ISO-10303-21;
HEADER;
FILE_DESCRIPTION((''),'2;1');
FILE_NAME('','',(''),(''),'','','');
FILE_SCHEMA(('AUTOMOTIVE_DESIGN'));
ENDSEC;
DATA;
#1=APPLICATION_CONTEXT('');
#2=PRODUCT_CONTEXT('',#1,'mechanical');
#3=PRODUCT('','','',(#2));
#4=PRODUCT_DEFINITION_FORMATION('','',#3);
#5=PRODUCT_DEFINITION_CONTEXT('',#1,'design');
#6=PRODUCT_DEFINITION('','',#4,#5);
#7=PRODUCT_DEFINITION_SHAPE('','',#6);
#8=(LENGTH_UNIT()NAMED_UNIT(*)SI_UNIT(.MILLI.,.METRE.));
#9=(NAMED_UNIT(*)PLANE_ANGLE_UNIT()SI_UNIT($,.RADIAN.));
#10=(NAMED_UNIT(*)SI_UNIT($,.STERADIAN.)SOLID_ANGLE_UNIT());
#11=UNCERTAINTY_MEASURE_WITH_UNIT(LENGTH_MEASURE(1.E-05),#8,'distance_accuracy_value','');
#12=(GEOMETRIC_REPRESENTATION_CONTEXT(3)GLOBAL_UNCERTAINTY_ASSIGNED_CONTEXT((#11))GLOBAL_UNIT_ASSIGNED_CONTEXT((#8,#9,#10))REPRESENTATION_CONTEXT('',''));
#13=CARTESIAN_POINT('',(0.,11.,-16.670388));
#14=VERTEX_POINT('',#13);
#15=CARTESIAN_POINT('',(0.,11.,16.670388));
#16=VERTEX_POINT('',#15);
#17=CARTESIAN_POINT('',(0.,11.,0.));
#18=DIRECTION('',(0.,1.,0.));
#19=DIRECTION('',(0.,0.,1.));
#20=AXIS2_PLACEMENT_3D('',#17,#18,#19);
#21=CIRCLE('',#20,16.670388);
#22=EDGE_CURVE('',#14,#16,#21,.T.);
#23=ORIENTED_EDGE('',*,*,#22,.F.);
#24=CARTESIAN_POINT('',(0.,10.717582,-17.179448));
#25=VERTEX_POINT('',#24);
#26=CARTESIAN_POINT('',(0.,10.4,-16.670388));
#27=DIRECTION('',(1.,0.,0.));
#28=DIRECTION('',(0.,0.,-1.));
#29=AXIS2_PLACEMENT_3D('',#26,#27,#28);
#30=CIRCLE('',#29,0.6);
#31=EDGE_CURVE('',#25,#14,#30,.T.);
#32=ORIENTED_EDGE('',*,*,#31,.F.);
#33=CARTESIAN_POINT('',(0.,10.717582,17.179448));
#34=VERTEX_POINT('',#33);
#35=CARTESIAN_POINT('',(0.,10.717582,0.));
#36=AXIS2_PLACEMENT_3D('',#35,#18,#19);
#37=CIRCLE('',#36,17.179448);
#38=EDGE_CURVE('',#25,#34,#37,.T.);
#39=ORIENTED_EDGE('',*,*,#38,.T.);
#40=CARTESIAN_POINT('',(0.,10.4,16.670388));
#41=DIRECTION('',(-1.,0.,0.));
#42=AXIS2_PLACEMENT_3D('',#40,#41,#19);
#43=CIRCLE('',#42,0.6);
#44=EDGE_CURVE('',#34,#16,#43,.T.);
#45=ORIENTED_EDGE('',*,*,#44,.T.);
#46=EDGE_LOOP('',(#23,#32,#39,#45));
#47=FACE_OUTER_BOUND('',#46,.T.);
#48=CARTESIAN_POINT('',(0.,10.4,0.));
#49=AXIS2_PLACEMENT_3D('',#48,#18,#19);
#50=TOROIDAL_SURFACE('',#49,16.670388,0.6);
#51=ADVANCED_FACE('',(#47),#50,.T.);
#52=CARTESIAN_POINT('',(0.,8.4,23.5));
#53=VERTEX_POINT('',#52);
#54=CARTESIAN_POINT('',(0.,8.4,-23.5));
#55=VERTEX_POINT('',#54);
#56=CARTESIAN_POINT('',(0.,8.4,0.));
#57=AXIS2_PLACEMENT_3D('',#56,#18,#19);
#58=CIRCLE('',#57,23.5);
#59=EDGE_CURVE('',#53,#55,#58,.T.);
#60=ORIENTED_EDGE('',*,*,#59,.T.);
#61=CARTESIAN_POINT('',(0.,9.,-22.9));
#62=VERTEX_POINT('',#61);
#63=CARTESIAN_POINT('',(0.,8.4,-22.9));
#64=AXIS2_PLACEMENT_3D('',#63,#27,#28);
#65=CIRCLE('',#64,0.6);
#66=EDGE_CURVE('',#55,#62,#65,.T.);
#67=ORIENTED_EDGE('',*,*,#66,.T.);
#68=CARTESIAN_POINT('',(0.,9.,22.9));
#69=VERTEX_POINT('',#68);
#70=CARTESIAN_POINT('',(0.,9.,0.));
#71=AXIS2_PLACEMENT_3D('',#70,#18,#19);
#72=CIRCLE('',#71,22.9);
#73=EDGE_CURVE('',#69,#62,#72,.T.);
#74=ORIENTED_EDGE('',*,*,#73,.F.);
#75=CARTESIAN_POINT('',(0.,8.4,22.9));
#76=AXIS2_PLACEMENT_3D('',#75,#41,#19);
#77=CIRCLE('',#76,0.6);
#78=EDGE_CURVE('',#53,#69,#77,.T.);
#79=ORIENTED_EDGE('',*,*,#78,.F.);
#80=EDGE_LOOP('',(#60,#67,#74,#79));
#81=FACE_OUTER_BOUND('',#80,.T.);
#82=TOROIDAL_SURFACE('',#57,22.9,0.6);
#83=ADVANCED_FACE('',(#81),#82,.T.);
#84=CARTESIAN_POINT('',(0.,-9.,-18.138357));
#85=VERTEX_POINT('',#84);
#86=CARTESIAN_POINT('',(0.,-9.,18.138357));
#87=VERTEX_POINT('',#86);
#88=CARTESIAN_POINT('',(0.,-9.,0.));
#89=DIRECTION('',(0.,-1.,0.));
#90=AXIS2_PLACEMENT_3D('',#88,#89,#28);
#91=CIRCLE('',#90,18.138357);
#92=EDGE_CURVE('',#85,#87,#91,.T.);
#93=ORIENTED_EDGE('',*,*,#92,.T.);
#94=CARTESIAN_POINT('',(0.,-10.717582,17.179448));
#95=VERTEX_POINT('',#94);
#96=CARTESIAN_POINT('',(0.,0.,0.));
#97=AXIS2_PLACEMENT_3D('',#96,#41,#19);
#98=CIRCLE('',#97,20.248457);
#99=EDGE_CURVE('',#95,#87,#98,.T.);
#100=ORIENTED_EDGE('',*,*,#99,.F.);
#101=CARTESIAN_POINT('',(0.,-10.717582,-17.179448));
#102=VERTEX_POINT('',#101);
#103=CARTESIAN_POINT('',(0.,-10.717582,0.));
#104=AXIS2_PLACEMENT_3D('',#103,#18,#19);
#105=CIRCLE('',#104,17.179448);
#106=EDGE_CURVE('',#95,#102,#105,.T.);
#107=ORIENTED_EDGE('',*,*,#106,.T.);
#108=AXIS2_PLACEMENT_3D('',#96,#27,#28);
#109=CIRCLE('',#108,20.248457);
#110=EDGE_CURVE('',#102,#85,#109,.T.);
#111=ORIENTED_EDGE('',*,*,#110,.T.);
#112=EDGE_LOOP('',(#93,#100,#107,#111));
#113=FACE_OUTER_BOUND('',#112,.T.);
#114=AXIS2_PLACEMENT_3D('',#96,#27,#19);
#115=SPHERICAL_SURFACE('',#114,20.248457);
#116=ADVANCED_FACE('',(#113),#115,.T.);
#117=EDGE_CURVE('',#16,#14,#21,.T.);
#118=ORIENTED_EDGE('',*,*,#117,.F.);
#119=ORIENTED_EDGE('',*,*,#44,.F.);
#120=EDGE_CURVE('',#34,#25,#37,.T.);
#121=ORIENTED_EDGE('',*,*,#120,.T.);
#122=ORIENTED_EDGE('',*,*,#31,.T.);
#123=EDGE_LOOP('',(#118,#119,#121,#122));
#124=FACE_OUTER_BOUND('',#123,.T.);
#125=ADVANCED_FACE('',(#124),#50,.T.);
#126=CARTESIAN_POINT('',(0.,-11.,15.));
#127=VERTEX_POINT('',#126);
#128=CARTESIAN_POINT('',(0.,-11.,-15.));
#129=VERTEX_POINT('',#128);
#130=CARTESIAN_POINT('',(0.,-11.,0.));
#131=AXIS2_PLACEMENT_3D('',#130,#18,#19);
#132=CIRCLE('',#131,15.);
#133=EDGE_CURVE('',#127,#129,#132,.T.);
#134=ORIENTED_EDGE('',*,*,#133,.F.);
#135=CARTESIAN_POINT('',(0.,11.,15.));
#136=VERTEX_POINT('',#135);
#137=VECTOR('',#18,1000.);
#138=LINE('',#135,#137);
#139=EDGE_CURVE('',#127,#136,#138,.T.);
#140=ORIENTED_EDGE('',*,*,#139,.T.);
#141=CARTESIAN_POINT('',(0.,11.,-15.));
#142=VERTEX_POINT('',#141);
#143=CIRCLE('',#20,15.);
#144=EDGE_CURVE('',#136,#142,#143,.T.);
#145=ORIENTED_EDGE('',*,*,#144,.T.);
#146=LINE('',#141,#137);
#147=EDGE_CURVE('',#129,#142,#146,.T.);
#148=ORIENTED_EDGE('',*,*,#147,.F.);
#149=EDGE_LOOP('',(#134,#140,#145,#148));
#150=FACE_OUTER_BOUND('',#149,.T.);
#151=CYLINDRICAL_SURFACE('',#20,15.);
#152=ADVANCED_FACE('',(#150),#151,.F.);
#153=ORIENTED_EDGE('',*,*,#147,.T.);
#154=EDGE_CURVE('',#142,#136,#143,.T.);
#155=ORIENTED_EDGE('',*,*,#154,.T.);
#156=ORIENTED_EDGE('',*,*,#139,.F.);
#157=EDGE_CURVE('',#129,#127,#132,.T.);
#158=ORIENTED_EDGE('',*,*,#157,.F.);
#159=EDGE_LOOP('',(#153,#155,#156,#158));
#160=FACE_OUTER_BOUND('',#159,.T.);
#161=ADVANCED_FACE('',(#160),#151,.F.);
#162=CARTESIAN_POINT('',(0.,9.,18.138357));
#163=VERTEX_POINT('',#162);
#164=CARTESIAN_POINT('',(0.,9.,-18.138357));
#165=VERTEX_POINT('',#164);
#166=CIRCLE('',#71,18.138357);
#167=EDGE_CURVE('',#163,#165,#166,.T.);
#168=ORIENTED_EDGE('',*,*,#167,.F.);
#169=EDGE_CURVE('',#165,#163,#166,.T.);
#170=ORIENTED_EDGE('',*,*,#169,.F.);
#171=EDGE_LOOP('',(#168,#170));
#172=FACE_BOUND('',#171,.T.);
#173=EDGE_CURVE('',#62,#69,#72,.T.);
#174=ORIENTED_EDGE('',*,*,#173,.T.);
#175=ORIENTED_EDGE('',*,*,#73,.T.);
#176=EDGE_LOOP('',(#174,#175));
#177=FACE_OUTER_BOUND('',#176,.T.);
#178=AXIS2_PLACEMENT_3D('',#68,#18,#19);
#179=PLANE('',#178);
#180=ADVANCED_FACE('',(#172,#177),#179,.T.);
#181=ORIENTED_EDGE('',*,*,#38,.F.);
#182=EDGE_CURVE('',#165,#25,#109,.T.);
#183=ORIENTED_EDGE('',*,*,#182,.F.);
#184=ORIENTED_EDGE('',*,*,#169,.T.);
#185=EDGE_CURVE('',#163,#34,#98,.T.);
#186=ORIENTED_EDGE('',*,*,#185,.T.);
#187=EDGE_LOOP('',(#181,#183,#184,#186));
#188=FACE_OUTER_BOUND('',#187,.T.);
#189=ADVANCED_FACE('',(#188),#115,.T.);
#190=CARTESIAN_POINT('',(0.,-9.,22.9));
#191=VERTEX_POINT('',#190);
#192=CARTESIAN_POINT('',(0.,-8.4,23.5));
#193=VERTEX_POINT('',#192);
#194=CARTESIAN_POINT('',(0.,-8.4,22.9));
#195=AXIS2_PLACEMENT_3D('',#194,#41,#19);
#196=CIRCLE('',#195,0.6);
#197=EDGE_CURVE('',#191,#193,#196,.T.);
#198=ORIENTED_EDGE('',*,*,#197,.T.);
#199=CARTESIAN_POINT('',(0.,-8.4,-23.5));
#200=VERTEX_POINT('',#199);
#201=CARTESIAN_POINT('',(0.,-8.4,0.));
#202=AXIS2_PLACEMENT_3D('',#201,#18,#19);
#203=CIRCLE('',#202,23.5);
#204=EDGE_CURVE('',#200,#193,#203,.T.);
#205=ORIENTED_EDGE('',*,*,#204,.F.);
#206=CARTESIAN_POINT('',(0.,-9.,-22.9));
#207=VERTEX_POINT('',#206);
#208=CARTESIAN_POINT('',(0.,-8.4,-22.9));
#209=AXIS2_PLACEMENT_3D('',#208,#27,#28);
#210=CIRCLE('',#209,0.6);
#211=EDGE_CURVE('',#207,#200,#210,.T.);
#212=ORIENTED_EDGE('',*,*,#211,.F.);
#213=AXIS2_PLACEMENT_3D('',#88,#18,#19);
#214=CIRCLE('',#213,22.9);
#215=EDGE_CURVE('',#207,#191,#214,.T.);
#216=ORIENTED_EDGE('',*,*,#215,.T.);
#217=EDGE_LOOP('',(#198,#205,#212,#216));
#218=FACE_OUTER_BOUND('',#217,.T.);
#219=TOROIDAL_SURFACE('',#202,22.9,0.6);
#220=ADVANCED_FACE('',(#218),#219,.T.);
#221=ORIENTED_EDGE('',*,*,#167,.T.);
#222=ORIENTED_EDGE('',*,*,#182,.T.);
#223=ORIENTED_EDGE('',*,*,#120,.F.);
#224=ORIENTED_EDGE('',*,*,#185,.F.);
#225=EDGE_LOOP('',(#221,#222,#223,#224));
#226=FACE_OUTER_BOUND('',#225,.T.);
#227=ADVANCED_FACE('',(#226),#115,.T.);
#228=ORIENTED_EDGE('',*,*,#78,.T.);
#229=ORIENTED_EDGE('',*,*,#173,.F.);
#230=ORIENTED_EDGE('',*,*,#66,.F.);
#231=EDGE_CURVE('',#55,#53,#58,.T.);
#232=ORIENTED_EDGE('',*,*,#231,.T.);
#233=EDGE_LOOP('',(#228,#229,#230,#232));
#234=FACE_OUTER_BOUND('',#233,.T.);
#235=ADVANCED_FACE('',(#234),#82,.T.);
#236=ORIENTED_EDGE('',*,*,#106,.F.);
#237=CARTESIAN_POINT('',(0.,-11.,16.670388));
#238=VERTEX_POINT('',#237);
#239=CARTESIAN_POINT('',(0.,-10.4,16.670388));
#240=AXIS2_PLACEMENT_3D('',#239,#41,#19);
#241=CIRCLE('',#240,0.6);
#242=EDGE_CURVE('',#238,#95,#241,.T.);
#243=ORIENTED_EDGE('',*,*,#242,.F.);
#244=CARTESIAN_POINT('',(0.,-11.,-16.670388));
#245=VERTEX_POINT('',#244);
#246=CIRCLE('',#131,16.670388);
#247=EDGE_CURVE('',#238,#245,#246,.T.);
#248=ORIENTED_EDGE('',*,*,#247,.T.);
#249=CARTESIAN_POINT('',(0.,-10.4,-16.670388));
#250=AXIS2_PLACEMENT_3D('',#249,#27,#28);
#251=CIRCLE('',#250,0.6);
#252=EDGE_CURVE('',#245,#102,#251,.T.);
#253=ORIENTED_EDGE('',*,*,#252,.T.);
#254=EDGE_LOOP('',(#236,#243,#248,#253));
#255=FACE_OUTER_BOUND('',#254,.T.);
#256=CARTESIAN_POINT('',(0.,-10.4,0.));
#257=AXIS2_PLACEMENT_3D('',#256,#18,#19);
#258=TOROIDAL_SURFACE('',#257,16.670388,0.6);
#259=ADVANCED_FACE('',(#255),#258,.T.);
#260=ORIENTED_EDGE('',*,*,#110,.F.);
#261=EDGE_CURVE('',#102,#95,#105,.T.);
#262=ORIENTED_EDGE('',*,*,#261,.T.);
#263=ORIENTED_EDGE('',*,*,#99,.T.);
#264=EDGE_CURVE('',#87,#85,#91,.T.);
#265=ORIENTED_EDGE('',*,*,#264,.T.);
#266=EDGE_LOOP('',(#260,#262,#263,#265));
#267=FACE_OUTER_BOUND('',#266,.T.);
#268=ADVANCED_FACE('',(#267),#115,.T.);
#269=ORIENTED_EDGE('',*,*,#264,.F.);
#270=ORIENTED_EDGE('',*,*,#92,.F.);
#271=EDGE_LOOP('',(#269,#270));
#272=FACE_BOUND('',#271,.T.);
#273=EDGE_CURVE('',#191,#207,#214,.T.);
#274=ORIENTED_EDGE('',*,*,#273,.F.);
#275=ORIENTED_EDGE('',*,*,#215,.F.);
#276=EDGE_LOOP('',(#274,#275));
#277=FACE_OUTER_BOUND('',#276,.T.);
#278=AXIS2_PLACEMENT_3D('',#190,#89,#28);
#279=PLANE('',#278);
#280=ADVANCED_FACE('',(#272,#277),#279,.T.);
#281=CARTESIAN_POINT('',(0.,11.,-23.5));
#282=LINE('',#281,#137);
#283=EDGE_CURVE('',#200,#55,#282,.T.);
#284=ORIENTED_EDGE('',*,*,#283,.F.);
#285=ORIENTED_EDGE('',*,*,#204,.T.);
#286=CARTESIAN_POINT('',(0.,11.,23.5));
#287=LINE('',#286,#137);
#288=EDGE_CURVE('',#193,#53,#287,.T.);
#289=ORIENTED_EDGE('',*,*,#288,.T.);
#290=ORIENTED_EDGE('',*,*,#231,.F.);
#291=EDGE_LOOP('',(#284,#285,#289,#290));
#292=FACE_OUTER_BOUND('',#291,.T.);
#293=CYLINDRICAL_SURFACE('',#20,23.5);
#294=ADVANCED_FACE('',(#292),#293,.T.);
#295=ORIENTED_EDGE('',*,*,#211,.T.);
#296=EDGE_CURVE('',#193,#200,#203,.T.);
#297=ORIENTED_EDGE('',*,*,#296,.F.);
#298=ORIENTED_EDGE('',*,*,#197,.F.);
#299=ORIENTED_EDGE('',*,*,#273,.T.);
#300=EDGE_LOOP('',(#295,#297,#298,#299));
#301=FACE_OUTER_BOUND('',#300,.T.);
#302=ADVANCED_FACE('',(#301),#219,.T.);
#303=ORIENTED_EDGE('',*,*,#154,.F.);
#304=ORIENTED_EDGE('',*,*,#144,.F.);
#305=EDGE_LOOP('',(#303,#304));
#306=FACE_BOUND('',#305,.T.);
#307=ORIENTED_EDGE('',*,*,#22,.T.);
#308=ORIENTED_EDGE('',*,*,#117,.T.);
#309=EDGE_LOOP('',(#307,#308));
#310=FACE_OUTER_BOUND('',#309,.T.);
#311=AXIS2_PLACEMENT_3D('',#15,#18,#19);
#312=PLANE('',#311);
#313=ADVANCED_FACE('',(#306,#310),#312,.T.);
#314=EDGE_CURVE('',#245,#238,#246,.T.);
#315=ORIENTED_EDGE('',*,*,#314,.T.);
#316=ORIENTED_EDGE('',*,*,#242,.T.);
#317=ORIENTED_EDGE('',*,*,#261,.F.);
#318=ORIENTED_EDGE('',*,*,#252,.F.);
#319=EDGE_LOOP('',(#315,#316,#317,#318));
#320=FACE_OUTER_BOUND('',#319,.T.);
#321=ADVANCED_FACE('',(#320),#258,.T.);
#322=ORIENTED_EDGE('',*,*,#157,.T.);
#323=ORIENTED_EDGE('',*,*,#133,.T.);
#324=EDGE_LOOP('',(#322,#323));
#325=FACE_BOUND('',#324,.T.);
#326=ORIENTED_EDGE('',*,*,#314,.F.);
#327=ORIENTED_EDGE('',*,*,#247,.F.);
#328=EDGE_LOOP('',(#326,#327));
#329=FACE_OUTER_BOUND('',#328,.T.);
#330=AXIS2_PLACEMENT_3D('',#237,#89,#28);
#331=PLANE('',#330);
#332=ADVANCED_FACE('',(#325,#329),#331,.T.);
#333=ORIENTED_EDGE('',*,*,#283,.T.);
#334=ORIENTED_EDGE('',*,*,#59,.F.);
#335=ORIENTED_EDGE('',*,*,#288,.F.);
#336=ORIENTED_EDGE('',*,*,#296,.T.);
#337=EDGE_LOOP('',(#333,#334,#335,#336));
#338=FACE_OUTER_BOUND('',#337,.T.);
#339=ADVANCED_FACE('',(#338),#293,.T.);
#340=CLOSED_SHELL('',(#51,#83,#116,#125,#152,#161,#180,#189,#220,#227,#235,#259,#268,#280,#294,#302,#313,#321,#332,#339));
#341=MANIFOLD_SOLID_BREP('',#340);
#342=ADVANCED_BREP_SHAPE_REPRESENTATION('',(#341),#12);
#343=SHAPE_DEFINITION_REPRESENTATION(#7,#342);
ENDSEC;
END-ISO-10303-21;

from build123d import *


with BuildPart() as part:
    # 草图2 → 旋转1 (revolve)
    with BuildSketch(Plane(origin=(0, 0, 0), x_dir=(0, 0, -1), z_dir=(1, 0, 0))):
        with BuildLine():
            Line((-22.9, 9), (-18.138357147, 9))
            ThreePointArc((-18.138357147, 9), (-20.248456731, 0), (-18.138357147, -9))
            Line((-18.138357147, -9), (-22.9, -9))
            ThreePointArc((-22.9, -9), (-23.324264069, -8.824264069), (-23.5, -8.4))
            Line((-23.5, -8.4), (-23.5, 8.4))
            ThreePointArc((-23.5, 8.4), (-23.324264069, 8.824264069), (-22.9, 9))
        make_face()
    revolve(axis=Axis((0, 11, 0), (0, -1, 0)))

    # 草图3 → 旋转2 (revolve)
    with BuildSketch(Plane(origin=(0, 0, 0), x_dir=(0, 0, -1), z_dir=(1, 0, 0))):
        with BuildLine():
            Line((-16.670388475, 11), (-15, 11))
            Line((-15, 11), (-15, -11))
            Line((-15, -11), (-16.670388475, -11))
            ThreePointArc((-16.670388475, -11), (-16.961464654, -10.924666235), (-17.179447951, -10.717582194))
            ThreePointArc((-17.179447951, -10.717582194), (-20.248456731, 0), (-17.179447951, 10.717582194))
            ThreePointArc((-17.179447951, 10.717582194), (-16.961464654, 10.924666235), (-16.670388475, 11))
        make_face()
    revolve(axis=Axis((0, 11, 0), (0, -1, 0)))


solid = part.part
